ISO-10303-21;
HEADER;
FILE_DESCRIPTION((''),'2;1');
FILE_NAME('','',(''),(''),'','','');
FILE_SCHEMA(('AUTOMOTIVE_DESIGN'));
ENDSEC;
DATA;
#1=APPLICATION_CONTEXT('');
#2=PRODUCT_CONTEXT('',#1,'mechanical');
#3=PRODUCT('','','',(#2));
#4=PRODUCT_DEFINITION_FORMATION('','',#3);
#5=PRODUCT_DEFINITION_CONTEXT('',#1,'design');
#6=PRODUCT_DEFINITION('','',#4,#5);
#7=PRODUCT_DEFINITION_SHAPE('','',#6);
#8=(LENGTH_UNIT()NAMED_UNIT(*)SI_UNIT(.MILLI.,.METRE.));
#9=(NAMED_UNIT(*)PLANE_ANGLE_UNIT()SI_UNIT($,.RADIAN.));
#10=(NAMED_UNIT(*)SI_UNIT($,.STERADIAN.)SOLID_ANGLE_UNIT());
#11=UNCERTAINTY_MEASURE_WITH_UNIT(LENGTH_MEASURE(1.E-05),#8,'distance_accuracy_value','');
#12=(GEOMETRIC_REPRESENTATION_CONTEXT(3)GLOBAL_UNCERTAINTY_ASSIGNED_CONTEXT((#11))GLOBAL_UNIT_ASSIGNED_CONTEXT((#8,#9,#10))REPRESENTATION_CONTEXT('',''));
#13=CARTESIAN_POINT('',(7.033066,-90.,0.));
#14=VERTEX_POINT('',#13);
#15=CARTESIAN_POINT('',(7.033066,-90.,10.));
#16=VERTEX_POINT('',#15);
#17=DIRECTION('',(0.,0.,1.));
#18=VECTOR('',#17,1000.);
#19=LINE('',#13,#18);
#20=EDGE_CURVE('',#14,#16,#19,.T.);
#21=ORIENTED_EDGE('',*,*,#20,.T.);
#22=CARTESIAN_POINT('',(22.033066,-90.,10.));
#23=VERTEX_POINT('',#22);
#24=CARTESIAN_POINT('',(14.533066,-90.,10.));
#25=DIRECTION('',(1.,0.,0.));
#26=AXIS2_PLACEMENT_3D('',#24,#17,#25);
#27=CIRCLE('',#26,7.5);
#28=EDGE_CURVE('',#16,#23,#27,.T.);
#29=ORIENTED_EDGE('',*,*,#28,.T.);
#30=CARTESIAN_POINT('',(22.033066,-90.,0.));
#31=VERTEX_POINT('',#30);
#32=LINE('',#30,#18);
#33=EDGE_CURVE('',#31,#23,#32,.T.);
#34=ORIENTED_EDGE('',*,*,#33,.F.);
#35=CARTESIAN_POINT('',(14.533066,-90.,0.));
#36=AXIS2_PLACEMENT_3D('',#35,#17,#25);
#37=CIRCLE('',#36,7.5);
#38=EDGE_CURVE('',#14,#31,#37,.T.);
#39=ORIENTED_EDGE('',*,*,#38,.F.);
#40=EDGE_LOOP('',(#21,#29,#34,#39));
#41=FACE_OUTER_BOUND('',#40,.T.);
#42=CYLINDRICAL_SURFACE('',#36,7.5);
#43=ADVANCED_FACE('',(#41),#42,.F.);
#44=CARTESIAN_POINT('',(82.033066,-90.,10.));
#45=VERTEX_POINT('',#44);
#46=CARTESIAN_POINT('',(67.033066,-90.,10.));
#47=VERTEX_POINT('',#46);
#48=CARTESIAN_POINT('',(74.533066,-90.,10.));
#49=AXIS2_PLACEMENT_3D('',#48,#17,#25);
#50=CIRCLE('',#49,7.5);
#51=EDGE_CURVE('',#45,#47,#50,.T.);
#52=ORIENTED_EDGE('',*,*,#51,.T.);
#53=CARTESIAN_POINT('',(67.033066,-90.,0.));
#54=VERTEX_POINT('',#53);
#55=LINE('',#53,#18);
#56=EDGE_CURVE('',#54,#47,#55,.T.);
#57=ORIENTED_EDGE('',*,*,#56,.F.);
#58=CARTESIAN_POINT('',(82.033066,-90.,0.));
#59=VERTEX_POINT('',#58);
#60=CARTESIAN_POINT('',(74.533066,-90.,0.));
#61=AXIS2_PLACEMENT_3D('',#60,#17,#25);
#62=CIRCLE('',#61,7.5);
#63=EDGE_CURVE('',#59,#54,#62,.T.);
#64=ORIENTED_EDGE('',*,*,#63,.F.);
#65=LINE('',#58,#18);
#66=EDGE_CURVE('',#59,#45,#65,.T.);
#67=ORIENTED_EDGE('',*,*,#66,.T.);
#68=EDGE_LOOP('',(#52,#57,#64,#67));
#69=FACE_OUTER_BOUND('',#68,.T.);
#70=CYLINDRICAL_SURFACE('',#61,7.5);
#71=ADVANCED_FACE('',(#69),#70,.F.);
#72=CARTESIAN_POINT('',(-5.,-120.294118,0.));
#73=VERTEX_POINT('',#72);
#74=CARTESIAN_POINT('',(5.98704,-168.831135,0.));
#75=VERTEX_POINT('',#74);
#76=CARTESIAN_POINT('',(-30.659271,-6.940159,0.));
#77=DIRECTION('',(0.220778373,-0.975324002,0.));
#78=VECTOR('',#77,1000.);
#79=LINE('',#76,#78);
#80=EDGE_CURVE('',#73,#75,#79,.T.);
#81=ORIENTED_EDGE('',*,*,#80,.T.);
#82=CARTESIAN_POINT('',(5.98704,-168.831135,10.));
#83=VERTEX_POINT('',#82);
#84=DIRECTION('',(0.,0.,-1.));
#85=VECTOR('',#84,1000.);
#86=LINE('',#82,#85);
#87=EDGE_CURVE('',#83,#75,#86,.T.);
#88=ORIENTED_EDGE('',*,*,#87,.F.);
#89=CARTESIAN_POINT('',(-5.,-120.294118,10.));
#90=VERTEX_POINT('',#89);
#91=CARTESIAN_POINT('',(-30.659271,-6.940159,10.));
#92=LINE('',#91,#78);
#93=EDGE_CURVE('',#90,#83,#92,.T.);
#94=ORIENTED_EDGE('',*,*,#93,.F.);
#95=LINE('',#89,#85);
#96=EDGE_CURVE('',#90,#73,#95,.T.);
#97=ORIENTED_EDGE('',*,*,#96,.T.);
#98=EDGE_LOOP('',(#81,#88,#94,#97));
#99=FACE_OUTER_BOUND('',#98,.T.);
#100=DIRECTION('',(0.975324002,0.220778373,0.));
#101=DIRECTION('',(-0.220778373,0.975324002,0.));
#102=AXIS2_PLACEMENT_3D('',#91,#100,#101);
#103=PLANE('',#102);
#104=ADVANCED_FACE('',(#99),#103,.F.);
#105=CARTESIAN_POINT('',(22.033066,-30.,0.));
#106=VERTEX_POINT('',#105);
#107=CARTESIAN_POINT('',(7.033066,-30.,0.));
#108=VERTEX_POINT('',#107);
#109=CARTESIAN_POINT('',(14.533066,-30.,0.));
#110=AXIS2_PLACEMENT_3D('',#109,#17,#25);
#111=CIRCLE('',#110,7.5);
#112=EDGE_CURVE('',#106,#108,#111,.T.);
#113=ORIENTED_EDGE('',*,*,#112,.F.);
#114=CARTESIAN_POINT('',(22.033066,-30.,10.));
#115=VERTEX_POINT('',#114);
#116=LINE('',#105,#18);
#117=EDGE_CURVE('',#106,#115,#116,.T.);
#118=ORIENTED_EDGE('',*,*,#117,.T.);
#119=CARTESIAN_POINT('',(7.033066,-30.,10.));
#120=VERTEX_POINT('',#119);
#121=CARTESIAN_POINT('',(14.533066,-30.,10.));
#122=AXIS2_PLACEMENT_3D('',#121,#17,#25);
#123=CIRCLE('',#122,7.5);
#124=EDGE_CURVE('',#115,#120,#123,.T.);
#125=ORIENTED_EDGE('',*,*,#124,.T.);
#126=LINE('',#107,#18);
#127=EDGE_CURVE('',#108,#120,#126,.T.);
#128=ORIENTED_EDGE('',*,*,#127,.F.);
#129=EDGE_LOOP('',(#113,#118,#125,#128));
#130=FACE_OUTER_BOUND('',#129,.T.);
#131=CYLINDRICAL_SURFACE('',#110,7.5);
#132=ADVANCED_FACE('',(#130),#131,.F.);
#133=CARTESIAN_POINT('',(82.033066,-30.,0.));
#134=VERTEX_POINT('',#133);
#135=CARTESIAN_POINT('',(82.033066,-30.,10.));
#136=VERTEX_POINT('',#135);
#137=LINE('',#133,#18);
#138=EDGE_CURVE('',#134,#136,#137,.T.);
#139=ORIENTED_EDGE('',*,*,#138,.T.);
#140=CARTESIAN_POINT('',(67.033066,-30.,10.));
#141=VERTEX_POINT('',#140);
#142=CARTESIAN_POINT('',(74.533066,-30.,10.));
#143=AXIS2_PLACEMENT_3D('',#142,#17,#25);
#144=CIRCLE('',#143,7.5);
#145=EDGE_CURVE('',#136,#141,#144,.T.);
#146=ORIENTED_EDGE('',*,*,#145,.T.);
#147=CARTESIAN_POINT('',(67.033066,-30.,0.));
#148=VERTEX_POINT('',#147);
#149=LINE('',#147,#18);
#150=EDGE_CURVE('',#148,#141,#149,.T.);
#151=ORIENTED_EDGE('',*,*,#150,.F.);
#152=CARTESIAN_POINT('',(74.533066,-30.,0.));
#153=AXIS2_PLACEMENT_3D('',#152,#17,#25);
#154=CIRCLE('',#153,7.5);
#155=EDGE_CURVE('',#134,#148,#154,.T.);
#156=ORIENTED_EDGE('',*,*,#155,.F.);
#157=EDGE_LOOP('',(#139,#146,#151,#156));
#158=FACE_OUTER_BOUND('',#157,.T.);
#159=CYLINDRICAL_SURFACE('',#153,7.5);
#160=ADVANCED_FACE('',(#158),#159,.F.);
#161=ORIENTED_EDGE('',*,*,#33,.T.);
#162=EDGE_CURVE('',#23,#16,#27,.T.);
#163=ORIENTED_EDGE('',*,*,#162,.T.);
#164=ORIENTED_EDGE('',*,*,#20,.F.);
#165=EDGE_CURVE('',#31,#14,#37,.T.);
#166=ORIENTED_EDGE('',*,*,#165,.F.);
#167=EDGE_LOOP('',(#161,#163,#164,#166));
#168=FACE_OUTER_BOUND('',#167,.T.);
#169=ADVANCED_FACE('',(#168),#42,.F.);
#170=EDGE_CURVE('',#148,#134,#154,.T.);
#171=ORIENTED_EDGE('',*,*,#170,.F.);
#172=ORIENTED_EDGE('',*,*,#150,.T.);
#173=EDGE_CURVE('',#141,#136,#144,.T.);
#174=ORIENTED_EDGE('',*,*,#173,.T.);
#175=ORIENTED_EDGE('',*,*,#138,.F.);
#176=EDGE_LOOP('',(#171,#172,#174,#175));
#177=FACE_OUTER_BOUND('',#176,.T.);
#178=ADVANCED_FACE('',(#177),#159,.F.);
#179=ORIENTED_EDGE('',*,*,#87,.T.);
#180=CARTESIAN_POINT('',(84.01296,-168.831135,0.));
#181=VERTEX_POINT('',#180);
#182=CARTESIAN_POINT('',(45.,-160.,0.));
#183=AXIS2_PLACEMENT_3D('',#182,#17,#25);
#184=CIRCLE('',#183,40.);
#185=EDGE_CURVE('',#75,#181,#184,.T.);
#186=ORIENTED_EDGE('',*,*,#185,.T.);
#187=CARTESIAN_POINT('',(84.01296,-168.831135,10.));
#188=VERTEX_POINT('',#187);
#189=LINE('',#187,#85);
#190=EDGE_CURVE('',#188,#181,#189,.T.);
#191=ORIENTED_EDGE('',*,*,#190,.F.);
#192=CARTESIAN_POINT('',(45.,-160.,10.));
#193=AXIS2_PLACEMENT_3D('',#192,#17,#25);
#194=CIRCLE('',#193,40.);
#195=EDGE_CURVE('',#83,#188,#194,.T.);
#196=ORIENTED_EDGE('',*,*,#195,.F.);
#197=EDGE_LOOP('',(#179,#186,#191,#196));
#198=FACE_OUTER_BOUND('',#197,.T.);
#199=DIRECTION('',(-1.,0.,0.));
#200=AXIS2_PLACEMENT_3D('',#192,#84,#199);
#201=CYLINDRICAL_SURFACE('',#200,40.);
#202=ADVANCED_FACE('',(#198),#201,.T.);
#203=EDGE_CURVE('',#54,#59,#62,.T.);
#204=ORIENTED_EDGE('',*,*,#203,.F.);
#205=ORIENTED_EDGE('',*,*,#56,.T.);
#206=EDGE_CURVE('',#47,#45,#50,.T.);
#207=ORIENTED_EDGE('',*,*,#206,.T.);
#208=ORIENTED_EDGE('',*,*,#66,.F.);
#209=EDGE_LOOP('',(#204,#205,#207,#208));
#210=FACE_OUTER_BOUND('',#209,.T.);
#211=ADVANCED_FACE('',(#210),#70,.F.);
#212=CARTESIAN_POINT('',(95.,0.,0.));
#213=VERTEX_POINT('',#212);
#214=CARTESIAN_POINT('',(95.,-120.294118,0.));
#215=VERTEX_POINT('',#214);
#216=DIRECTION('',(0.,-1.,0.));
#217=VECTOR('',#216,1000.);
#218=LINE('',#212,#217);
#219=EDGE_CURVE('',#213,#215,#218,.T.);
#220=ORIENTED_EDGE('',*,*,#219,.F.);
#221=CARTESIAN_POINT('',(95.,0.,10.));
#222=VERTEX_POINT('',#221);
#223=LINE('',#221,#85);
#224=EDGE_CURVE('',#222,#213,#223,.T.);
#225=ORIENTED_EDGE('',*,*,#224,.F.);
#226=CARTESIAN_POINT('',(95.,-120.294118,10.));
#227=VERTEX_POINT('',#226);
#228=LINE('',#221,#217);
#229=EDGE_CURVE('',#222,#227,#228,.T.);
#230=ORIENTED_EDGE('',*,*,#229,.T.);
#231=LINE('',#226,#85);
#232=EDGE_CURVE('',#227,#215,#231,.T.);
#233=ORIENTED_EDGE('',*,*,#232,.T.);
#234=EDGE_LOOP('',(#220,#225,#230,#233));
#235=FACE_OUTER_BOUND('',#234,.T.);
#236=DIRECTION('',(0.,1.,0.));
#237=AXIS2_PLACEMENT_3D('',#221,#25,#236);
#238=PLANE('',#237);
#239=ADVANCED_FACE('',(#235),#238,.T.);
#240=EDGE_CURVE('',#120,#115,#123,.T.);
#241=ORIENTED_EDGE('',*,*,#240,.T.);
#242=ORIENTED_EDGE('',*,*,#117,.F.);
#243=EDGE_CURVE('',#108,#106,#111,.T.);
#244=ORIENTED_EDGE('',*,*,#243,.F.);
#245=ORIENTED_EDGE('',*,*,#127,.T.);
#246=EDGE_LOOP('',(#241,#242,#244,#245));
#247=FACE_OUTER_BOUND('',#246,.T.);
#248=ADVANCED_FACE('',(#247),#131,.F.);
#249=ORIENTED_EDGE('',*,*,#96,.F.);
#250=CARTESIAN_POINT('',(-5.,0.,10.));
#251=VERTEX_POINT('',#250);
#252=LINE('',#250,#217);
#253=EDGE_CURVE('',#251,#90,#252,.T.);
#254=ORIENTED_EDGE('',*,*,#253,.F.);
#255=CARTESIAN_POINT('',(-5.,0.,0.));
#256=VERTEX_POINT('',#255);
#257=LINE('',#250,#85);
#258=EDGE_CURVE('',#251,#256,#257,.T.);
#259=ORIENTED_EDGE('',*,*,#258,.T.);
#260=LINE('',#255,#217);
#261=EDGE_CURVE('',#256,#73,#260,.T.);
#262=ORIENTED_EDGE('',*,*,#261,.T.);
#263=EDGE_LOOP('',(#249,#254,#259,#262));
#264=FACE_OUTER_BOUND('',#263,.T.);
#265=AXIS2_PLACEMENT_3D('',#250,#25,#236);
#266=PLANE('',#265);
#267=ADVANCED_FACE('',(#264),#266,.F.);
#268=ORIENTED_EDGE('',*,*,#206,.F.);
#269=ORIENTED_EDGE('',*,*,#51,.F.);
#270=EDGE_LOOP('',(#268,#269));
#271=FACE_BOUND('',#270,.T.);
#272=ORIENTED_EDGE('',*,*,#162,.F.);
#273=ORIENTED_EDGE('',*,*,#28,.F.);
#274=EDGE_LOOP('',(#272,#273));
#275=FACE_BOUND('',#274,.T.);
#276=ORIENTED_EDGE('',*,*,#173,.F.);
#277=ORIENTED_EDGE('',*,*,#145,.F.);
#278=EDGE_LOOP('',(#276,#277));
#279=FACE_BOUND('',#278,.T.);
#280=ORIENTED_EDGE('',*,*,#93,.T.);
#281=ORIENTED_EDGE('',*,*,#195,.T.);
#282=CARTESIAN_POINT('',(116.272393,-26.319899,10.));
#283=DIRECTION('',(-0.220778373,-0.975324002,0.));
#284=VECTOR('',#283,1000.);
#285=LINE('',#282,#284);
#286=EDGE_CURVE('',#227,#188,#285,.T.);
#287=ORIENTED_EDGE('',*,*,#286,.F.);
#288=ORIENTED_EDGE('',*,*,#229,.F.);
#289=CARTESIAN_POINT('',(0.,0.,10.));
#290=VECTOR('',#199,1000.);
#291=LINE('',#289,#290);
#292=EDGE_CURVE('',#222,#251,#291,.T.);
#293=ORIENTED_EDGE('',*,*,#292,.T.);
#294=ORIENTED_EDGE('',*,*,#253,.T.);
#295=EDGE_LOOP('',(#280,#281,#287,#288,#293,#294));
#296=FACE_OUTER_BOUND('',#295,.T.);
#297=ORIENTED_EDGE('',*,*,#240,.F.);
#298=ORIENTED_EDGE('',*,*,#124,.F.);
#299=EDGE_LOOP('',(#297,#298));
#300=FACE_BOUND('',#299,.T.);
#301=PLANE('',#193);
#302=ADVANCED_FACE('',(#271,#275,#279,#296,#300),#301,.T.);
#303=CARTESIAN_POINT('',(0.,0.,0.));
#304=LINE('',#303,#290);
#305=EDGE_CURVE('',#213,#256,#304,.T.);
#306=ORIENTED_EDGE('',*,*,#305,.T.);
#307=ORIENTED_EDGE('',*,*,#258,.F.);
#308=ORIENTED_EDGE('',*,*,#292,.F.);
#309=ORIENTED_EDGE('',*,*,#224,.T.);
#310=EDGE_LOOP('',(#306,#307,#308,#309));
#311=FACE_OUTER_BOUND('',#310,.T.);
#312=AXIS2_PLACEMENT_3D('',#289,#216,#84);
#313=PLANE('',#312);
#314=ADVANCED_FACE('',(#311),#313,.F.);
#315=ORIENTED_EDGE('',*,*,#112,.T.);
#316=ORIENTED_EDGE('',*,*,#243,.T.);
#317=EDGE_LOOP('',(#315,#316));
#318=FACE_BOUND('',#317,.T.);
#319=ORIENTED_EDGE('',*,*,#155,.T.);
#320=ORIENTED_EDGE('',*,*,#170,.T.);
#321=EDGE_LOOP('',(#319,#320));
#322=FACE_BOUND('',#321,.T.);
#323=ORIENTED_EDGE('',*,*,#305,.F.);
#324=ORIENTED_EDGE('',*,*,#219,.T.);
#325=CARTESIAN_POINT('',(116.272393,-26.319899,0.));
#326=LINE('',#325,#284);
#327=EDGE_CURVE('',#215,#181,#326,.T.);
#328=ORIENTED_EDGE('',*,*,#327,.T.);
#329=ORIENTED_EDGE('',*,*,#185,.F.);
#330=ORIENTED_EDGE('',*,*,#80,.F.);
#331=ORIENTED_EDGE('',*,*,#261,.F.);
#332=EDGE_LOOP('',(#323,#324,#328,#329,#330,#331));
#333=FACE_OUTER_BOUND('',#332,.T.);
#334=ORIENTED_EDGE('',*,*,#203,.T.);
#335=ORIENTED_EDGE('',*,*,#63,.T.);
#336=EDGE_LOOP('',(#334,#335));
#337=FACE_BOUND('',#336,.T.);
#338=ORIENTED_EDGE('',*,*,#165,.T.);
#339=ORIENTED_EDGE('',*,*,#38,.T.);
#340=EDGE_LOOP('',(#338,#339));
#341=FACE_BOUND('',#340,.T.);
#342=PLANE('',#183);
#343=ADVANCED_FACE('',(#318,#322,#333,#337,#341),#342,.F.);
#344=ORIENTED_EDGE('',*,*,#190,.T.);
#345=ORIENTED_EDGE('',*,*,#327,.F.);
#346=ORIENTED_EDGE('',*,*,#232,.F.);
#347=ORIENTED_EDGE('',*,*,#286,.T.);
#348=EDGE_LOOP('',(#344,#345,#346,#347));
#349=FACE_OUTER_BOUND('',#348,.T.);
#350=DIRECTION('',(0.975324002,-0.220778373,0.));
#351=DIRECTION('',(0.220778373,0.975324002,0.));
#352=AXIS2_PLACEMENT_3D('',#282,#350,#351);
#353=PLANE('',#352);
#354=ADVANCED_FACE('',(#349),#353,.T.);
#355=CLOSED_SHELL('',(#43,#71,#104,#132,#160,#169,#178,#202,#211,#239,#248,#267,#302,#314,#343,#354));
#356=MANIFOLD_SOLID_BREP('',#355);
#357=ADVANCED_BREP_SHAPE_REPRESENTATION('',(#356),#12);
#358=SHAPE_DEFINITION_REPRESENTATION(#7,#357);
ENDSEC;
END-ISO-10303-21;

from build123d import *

# Parameters (mm, degrees)
SKETCH_1_R          = 20
EXTRUDE_1_DEPTH     = 10
CUT_EXTRUDE_1_DEPTH = 10
EXTRUDE_START       = -10
EXTRUDE_4_DEPTH     = 10
EXTRUDE_8_DEPTH     = 10
SKETCH_5_R          = 22.505017269
EXTRUDE_9_DEPTH     = 10


with BuildPart() as part:
    # 草图1 → 凸台-拉伸1 (new body)
    with BuildSketch(Plane.XY):
        with BuildLine():
            Line((0, 0), (90, 0))
            Line((90, 0), (84.980633901, -161.244553285))
            ThreePointArc((84.980633901, -161.244553285), (45, -200), (5.019366099, -161.244553285))
            Line((5.019366099, -161.244553285), (0, 0))
        make_face()
        with Locations((45, -160)):
            Circle(SKETCH_1_R, mode=Mode.SUBTRACT)
    extrude(amount=EXTRUDE_1_DEPTH)

    # 草图2 → 切除-拉伸1 (cut)
    with BuildSketch(Plane.XY.offset(10)):
        with BuildLine():
            Line((7.033066451, -30), (14.533066451, -30))
            Line((14.533066451, -30), (22.033066451, -30))
            ThreePointArc((22.033066451, -30), (14.533066451, -22.5), (7.033066451, -30))
        make_face()
        with BuildLine():
            Line((22.033066451, -30), (14.533066451, -30))
            Line((14.533066451, -30), (14.533066451, -37.5))
            ThreePointArc((14.533066451, -37.5), (19.83636731, -35.303300859), (22.033066451, -30))
        make_face()
        with BuildLine():
            Line((14.533066451, -37.5), (14.533066451, -30))
            Line((14.533066451, -30), (7.033066451, -30))
            ThreePointArc((7.033066451, -30), (9.229765592, -35.303300859), (14.533066451, -37.5))
        make_face()
        with BuildLine():
            Line((67.033066451, -30), (74.533066451, -30))
            Line((74.533066451, -30), (82.033066451, -30))
            ThreePointArc((82.033066451, -30), (74.533066451, -22.5), (67.033066451, -30))
        make_face()
        with BuildLine():
            ThreePointArc((67.033066451, -30), (69.229765592, -35.303300859), (74.533066451, -37.5))
            Line((74.533066451, -37.5), (74.533066451, -30))
            Line((74.533066451, -30), (67.033066451, -30))
        make_face()
        with BuildLine():
            Line((74.533066451, -30), (74.533066451, -37.5))
            ThreePointArc((74.533066451, -37.5), (79.83636731, -35.303300859), (82.033066451, -30))
            Line((82.033066451, -30), (74.533066451, -30))
        make_face()
        with BuildLine():
            ThreePointArc((74.533066451, -82.5), (69.229765592, -84.696699141), (67.033066451, -90))
            Line((67.033066451, -90), (74.533066451, -90))
            Line((74.533066451, -90), (74.533066451, -82.5))
        make_face()
        with BuildLine():
            Line((74.533066451, -90), (67.033066451, -90))
            ThreePointArc((67.033066451, -90), (74.533066451, -97.5), (82.033066451, -90))
            ThreePointArc((82.033066451, -90), (79.83636731, -84.696699141), (74.533066451, -82.5))
            Line((74.533066451, -82.5), (74.533066451, -90))
        make_face()
        with BuildLine():
            ThreePointArc((22.033066451, -90), (19.83636731, -84.696699141), (14.533066451, -82.5))
            Line((14.533066451, -82.5), (14.533066451, -90))
            Line((14.533066451, -90), (22.033066451, -90))
        make_face()
        with BuildLine():
            Line((14.533066451, -90), (14.533066451, -82.5))
            ThreePointArc((14.533066451, -82.5), (9.229765592, -95.303300859), (22.033066451, -90))
            Line((22.033066451, -90), (14.533066451, -90))
        make_face()
    extrude(amount=-CUT_EXTRUDE_1_DEPTH, mode=Mode.SUBTRACT)

    # 草图3 → 凸台-拉伸4 (add)
    with BuildSketch(Plane.XY.offset(10).offset(EXTRUDE_START)):
        with BuildLine():
            Line((5.019366099, -161.244553285), (0, 0))
            Line((0, 0), (0, -120))
            Line((0, -120), (5.275862069, -164.689655172))
            ThreePointArc((5.275862069, -164.689655172), (5.110404302, -162.969874585), (5.019366099, -161.244553285))
        make_face()
        with BuildLine():
            Line((90, 0), (84.980633901, -161.244553285))
            ThreePointArc((84.980633901, -161.244553285), (84.889595698, -162.969874585), (84.724137931, -164.689655172))
            Line((84.724137931, -164.689655172), (90, -120))
            Line((90, -120), (90, 0))
        make_face()
    extrude(amount=EXTRUDE_4_DEPTH)

    # 草图4 → 凸台-拉伸8 (add)
    with BuildSketch(Plane(origin=(0, 0, 0), x_dir=(-1, 0, 0), z_dir=(0, 0, -1))):
        with BuildLine():
            Line((-90, -120), (-90, 0))
            Line((-90, 0), (-95, 0))
            Line((-95, 0), (-95, -120.294117647))
            Line((-95, -120.294117647), (-84.012960099, -168.831134939))
            ThreePointArc((-84.012960099, -168.831134939), (-84.422970654, -166.769740378), (-84.724137931, -164.689655172))
            Line((-84.724137931, -164.689655172), (-90, -120))
        make_face()
        with BuildLine():
            Line((5, 0), (0, 0))
            Line((0, 0), (0, -120))
            Line((0, -120), (-5.275862069, -164.689655172))
            ThreePointArc((-5.275862069, -164.689655172), (-5.577029346, -166.769740378), (-5.987039901, -168.831134939))
            Line((-5.987039901, -168.831134939), (5, -120.294117647))
            Line((5, -120.294117647), (5, 0))
        make_face()
    extrude(amount=-EXTRUDE_8_DEPTH)

    # 草图5 → 凸台-拉伸9 (add)
    with BuildSketch(Plane(origin=(0, 0, 0), x_dir=(-1, 0, 0), z_dir=(0, 0, -1))):
        with Locations((-45, -160)):
            Circle(SKETCH_5_R)
    extrude(amount=-EXTRUDE_9_DEPTH)


solid = part.part
